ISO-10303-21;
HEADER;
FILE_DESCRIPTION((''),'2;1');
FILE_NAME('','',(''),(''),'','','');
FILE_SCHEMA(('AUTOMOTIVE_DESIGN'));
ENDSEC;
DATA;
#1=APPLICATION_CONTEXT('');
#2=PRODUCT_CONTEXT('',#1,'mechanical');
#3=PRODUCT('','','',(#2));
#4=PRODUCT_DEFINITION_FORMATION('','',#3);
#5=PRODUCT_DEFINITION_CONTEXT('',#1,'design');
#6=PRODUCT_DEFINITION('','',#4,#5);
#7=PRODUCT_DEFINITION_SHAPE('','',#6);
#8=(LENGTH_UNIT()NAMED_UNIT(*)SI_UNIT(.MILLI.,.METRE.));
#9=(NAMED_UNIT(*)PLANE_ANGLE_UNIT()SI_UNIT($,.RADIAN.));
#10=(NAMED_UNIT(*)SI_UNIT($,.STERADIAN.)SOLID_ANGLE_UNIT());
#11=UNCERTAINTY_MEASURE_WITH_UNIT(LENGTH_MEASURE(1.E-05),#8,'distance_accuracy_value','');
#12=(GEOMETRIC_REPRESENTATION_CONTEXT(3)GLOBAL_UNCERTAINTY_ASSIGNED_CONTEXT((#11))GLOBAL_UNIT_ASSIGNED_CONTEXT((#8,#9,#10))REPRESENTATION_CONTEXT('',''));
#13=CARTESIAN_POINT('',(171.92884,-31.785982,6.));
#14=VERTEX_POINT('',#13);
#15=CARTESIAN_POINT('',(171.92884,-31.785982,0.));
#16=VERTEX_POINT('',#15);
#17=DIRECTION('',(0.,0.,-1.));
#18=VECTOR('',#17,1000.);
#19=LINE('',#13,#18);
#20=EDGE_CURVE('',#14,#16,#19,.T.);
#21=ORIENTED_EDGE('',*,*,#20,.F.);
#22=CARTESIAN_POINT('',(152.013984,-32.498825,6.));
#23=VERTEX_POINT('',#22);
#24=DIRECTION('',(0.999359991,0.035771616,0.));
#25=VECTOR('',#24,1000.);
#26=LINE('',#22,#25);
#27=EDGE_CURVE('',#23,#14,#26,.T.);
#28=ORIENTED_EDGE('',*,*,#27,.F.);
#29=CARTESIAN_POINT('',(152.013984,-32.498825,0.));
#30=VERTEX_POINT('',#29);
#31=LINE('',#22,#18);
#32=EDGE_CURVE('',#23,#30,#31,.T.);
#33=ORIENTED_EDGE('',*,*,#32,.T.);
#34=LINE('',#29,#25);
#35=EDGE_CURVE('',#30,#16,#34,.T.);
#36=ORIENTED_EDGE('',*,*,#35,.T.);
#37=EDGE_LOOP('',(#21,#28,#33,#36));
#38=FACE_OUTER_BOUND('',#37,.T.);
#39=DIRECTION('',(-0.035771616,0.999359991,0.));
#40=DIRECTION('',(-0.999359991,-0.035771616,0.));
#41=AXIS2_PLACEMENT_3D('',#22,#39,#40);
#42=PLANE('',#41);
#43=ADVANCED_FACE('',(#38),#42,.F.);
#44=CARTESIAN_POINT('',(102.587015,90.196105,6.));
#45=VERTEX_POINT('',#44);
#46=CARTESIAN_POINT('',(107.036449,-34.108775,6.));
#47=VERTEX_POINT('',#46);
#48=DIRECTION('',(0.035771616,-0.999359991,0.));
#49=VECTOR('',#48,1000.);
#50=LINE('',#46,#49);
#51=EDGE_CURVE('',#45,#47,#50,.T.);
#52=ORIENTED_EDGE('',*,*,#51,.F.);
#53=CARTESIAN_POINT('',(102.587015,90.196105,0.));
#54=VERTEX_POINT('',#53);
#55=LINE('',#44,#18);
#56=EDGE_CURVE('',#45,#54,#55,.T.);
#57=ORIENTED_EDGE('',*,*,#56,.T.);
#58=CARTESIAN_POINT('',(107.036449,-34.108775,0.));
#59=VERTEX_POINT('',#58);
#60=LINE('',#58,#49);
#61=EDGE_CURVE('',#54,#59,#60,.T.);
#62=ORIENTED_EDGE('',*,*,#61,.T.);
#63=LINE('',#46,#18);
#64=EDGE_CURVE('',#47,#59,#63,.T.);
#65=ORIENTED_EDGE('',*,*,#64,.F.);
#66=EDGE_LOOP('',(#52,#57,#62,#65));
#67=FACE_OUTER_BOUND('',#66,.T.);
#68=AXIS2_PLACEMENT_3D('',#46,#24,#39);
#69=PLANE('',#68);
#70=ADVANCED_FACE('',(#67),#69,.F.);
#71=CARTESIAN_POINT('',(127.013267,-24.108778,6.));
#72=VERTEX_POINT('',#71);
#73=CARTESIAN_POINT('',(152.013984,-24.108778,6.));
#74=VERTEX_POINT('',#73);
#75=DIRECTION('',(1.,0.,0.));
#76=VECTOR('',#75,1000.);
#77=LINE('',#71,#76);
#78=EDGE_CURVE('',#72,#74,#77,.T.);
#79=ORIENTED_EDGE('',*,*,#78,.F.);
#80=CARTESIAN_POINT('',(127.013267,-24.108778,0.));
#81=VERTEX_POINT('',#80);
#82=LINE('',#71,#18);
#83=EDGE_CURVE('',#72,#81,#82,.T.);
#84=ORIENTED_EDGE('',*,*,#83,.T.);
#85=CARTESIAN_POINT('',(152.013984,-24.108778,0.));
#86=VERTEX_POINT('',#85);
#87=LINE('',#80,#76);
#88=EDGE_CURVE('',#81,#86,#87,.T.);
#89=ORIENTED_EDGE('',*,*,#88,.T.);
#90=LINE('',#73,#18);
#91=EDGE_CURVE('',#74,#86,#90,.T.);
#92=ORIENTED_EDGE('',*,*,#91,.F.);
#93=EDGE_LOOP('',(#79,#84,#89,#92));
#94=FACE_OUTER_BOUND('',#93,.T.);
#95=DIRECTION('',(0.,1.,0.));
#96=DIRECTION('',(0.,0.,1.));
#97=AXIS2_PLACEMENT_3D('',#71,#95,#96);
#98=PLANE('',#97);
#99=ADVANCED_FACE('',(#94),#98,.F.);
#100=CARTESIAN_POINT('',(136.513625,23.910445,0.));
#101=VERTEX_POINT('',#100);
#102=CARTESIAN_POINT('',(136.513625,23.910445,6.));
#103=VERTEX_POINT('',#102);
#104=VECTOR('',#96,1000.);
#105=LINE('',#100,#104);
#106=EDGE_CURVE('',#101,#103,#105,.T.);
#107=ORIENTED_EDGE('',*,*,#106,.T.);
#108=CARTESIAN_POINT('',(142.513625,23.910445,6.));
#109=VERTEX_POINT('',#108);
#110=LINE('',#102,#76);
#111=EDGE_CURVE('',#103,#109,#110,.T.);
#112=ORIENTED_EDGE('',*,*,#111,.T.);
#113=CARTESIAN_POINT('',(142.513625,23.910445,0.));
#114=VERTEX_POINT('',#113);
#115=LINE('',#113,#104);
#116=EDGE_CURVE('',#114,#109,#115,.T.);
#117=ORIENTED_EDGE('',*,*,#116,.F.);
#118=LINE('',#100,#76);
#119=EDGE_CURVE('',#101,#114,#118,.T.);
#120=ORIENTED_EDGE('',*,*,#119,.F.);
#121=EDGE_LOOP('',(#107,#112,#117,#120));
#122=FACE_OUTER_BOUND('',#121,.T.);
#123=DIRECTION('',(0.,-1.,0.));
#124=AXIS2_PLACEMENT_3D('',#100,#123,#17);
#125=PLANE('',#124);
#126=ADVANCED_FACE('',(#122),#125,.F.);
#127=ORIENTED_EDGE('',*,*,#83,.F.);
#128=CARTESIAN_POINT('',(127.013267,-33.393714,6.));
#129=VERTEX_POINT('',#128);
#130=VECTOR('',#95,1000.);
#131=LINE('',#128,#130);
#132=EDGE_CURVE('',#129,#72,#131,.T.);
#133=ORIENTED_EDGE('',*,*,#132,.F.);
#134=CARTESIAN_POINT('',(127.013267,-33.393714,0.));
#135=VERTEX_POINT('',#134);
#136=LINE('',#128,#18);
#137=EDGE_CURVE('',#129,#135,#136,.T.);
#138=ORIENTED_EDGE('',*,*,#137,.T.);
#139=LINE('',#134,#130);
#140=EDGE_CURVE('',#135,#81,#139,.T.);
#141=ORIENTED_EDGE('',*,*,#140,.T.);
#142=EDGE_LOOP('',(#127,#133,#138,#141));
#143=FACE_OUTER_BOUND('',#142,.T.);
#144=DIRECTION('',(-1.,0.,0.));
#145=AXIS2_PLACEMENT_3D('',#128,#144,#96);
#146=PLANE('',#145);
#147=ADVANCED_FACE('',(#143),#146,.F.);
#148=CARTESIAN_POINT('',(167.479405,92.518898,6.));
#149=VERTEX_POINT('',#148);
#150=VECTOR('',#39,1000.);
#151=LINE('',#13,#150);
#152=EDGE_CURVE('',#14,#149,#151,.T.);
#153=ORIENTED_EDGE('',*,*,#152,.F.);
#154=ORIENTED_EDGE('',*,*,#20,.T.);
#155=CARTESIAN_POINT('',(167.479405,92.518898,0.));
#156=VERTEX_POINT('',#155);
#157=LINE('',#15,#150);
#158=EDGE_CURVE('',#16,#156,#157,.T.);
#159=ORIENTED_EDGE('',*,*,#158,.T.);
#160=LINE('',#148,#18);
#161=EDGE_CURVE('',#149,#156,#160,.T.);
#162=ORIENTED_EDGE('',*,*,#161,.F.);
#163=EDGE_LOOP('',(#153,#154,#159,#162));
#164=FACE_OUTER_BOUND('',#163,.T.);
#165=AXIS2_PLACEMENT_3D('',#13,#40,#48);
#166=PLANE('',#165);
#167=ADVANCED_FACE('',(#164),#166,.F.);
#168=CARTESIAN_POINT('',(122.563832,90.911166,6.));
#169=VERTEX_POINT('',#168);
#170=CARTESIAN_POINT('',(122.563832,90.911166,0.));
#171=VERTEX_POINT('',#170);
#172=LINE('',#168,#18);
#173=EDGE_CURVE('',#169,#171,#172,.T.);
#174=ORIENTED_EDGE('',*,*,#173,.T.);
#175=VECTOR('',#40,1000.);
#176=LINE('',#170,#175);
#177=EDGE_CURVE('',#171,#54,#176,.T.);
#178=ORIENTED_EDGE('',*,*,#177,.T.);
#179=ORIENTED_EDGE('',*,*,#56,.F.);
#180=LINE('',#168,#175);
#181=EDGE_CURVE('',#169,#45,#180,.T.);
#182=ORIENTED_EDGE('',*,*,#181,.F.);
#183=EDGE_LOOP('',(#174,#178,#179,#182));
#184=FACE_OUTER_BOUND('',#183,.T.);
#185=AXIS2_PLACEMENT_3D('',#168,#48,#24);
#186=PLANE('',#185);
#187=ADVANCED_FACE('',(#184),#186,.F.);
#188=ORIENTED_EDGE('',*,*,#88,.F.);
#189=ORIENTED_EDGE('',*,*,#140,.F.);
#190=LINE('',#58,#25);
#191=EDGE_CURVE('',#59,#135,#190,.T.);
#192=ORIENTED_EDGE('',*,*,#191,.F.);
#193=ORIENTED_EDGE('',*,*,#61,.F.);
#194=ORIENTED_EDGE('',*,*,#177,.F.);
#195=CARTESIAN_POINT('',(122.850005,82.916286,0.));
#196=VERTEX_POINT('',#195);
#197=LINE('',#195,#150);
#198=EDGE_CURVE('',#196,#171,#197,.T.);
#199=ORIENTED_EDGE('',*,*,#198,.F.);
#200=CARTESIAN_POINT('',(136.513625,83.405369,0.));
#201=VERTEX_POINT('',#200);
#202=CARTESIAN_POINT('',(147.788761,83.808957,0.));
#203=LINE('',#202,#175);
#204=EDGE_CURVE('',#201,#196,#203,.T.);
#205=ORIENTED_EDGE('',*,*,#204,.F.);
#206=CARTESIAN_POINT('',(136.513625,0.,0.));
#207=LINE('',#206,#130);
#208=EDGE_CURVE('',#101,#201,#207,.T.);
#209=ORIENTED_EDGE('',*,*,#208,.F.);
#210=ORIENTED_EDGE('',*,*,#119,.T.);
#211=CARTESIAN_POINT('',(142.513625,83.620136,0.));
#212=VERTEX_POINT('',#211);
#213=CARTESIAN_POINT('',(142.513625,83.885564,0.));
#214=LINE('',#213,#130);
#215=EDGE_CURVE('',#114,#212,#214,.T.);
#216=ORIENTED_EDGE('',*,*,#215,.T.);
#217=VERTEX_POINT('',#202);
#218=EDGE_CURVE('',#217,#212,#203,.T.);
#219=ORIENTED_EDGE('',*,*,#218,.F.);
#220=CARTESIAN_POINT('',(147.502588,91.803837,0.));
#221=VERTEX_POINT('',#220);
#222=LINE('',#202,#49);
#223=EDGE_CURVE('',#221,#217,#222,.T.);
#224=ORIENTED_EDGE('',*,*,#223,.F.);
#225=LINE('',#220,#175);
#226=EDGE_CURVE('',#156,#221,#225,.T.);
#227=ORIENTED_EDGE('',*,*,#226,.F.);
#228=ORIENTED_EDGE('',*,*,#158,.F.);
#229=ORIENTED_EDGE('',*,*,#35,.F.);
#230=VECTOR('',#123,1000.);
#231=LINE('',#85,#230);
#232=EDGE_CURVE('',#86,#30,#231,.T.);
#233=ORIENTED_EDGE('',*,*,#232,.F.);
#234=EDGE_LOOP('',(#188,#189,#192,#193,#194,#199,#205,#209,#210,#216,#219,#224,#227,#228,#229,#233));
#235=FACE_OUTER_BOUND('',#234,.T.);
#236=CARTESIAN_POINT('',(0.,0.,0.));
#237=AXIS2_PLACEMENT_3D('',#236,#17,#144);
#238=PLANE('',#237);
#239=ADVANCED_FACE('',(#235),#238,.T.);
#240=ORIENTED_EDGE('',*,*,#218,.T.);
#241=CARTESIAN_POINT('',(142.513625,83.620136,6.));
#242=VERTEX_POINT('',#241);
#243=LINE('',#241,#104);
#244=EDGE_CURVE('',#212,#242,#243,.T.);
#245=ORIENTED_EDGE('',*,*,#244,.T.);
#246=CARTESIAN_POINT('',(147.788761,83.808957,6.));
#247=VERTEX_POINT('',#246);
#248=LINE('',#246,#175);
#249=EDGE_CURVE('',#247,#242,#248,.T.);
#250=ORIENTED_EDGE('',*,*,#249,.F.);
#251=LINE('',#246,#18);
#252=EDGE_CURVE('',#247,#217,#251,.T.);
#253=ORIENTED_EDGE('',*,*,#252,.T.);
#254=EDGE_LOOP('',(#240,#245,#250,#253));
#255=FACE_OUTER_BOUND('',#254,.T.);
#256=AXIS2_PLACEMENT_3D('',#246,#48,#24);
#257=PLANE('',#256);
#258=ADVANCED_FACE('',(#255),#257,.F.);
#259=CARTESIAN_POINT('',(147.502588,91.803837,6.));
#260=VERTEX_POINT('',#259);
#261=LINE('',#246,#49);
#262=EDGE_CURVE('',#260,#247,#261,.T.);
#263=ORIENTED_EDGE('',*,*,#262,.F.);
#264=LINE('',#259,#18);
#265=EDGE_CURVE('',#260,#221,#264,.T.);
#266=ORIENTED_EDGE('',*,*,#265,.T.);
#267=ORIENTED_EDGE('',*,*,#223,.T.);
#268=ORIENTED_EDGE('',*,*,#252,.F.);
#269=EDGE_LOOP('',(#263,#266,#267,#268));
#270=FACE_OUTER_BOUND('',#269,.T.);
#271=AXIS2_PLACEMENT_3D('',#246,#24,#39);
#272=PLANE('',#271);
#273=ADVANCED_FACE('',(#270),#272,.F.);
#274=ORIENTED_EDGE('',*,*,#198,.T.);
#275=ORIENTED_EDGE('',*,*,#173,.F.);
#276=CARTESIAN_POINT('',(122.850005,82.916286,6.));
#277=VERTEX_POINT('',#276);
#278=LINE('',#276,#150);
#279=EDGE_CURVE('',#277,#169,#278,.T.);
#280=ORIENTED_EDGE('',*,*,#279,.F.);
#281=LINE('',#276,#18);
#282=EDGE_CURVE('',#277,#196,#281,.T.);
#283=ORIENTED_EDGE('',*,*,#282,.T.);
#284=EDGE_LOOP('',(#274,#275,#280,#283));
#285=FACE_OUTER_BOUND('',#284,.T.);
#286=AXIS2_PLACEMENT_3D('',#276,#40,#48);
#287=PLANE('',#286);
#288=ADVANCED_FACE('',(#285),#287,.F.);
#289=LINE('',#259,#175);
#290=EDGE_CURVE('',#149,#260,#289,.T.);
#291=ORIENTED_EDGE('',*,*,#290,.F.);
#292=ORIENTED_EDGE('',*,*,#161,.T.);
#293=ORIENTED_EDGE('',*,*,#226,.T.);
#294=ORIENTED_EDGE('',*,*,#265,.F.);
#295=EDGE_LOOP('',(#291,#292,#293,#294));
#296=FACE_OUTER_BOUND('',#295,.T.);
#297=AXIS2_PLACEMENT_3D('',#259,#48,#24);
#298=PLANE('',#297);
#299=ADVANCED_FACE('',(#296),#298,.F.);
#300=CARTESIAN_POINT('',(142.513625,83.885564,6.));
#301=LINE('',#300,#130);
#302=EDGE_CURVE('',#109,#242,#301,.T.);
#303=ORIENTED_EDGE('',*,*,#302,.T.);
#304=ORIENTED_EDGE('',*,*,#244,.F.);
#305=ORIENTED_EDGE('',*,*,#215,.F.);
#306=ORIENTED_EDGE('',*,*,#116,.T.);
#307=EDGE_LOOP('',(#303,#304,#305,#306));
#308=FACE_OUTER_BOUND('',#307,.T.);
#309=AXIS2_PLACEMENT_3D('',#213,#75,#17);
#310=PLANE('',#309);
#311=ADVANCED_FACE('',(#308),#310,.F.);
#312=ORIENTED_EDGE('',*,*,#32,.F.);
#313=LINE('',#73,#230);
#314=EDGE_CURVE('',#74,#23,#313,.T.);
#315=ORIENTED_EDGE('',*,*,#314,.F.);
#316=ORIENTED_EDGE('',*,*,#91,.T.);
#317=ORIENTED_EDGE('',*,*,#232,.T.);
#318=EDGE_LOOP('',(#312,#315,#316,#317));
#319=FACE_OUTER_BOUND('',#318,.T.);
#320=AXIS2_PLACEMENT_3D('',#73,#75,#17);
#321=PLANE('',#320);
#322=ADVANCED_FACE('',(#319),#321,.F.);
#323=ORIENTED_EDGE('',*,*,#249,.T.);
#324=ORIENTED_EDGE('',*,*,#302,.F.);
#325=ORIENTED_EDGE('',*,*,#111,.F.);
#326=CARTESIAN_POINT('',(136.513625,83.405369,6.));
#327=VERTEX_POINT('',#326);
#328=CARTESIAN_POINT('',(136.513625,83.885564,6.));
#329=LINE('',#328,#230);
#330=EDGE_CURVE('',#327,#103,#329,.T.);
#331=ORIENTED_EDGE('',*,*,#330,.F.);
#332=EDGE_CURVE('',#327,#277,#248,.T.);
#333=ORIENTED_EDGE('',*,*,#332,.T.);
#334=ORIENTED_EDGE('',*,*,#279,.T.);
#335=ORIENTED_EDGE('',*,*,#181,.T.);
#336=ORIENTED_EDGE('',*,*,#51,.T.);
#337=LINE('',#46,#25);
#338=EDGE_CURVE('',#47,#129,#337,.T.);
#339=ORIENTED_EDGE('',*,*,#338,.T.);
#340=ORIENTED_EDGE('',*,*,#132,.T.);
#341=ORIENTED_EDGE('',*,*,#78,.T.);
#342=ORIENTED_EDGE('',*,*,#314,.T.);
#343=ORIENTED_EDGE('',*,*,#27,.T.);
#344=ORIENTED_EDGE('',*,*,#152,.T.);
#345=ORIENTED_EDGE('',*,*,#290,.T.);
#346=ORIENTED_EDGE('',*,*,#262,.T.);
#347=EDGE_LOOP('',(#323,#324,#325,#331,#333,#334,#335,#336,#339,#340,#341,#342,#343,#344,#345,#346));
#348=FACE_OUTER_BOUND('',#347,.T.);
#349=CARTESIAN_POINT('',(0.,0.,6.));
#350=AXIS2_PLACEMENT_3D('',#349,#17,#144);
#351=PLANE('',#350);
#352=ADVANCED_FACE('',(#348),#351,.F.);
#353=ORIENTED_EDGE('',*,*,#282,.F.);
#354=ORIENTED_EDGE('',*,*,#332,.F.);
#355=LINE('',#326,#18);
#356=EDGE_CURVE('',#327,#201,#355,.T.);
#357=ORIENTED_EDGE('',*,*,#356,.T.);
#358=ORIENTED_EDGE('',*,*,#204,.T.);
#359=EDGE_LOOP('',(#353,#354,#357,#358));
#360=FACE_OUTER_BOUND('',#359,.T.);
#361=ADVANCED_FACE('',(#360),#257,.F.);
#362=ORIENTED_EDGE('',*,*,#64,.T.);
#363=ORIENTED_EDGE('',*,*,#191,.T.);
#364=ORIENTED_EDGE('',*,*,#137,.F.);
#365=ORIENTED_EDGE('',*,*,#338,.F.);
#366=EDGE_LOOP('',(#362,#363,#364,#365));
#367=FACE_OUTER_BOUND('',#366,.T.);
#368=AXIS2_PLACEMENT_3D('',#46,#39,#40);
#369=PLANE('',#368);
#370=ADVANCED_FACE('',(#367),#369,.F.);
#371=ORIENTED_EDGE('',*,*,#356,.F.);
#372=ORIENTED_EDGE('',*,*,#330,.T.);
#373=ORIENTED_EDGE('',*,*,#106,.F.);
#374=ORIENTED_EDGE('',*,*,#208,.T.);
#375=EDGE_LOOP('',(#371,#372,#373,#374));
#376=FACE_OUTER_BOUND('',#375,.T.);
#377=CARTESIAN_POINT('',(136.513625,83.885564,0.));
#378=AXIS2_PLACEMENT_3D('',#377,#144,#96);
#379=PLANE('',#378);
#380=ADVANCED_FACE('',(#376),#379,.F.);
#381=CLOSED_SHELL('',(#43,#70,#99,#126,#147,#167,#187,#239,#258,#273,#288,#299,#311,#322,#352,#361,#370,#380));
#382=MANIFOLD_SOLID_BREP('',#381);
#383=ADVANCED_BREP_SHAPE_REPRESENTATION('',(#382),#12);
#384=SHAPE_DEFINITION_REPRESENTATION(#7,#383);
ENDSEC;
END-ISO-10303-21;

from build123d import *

# Parameters (mm, degrees)
BOSS_EXTRUDE1_DEPTH = 6
SKETCH2_W           = 6
SKETCH2_H           = 59.975118876
CUT_EXTRUDE1_DEPTH  = 6


with BuildPart() as part:
    # Sketch1 → Boss-Extrude1 (new body)
    with BuildSketch(Plane.XY):
        Polygon((107.036449202, -34.108774603), (102.587015051, 90.196105325), (122.563832413, 90.911166016), (122.850005344, 82.916286089), (147.788760974, 83.808957004), (147.502588043, 91.803836932), (167.479405405, 92.518897623), (171.928839556, -31.785982304), (152.013983639, -32.498825115), (152.013983639, -24.108777743), (127.013266564, -24.108777743), (127.013266564, -33.393713911), align=None)
    extrude(amount=BOSS_EXTRUDE1_DEPTH)

    # Sketch2 → Cut-Extrude1 (cut)
    with BuildSketch(Plane.XY.offset(6)):
        with Locations((139.513625101, 53.898004923)):
            Rectangle(SKETCH2_W, SKETCH2_H)
    extrude(amount=-CUT_EXTRUDE1_DEPTH, mode=Mode.SUBTRACT)


solid = part.part
